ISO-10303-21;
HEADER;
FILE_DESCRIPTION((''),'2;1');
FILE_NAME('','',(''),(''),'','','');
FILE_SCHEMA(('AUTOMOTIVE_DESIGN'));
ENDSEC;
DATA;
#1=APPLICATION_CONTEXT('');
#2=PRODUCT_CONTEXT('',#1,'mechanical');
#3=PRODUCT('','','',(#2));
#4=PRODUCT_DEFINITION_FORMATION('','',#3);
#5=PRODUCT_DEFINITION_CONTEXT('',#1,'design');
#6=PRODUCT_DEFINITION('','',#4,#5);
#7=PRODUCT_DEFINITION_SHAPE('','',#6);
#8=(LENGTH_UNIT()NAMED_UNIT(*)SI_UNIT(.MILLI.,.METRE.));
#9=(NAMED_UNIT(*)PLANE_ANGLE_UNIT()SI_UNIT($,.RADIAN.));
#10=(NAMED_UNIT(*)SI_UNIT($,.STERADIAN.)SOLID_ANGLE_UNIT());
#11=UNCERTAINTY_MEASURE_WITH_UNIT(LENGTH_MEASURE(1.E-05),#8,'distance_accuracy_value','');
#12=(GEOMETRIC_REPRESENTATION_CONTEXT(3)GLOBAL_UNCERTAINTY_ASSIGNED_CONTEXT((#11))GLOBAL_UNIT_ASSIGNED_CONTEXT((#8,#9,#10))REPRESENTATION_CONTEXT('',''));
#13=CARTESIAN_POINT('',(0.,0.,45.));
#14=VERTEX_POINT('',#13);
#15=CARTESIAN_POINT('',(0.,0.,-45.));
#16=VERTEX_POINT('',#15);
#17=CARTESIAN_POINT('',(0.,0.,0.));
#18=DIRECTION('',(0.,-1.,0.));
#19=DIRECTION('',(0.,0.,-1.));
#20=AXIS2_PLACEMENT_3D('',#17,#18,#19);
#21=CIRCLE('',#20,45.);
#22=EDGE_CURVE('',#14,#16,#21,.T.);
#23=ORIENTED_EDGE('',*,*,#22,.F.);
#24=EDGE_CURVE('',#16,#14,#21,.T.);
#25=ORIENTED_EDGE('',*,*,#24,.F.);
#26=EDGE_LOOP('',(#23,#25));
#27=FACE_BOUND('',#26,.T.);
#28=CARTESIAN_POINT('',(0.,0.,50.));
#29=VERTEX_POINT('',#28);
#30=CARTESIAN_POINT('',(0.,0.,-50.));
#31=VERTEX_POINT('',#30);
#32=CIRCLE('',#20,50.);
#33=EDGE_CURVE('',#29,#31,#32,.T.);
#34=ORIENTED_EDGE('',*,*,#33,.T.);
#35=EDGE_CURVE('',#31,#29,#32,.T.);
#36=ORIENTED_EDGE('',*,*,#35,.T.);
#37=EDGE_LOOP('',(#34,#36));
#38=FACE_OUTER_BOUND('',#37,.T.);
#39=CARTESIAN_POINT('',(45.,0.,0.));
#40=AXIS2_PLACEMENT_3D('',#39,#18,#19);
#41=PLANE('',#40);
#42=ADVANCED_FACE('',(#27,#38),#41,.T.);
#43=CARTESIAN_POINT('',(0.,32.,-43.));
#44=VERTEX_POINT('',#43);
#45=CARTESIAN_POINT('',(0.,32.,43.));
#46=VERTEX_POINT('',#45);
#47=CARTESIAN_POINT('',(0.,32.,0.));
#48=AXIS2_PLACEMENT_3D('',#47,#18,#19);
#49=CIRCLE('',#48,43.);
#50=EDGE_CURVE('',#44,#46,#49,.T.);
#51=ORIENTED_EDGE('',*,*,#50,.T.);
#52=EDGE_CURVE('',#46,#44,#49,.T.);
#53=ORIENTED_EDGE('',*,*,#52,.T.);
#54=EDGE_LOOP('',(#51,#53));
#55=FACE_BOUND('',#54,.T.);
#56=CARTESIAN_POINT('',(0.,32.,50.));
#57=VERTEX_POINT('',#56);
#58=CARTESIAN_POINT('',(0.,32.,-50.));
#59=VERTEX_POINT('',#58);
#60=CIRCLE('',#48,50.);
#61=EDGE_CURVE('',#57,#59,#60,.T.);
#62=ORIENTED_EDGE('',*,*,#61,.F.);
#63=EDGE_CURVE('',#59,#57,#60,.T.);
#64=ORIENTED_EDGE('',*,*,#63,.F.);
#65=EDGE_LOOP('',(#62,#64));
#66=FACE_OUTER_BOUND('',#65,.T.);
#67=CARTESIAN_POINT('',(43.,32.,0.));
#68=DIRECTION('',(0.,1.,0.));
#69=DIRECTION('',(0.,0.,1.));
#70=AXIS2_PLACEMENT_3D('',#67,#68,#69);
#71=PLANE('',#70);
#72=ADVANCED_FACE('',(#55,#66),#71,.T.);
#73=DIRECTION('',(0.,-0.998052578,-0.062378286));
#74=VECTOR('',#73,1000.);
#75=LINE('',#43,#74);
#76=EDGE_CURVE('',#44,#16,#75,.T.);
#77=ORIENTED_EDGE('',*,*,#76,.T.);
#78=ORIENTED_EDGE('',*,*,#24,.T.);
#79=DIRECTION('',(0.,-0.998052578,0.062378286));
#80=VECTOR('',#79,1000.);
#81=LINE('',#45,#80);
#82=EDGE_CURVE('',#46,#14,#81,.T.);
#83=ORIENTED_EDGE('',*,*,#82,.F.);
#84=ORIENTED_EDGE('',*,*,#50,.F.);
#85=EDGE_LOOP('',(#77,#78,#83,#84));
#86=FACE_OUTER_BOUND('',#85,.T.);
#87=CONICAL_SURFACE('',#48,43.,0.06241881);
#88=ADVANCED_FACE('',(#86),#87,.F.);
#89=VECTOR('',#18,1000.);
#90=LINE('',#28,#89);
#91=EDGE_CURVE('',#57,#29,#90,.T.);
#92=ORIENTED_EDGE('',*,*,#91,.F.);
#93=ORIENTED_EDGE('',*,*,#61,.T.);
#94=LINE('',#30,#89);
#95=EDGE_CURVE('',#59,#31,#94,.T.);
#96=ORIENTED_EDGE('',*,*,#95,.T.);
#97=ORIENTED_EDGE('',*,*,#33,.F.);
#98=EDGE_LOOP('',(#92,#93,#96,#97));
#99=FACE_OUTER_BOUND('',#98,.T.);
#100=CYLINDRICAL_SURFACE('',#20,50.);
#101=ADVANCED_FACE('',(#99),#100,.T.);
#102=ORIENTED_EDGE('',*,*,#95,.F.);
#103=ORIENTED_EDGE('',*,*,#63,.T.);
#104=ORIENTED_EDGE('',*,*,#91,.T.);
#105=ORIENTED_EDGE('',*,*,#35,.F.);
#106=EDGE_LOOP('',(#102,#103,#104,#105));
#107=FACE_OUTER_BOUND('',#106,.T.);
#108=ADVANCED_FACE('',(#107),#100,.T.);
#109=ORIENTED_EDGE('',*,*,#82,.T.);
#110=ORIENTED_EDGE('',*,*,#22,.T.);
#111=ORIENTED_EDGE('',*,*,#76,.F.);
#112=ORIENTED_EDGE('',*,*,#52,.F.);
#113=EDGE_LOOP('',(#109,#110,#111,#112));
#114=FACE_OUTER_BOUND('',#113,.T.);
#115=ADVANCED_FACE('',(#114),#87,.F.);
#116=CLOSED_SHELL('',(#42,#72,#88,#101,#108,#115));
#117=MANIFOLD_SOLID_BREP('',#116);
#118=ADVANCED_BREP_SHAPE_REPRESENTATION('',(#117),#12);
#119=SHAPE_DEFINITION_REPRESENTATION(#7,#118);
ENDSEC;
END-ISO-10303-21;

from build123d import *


with BuildPart() as part:
    # Sketch2 → Revolve1 (revolve)
    with BuildSketch(Plane.XY, mode=Mode.PRIVATE) as revolve1_sk:
        Polygon((43, 32), (45, 0), (50, 0), (50, 32), align=None)
    revolve(revolve1_sk.sketch.rotate(Axis((0, 0, 0), (0, 1, 0)), 90), axis=Axis((0, 0, 0), (0, 1, 0)))


solid = part.part
